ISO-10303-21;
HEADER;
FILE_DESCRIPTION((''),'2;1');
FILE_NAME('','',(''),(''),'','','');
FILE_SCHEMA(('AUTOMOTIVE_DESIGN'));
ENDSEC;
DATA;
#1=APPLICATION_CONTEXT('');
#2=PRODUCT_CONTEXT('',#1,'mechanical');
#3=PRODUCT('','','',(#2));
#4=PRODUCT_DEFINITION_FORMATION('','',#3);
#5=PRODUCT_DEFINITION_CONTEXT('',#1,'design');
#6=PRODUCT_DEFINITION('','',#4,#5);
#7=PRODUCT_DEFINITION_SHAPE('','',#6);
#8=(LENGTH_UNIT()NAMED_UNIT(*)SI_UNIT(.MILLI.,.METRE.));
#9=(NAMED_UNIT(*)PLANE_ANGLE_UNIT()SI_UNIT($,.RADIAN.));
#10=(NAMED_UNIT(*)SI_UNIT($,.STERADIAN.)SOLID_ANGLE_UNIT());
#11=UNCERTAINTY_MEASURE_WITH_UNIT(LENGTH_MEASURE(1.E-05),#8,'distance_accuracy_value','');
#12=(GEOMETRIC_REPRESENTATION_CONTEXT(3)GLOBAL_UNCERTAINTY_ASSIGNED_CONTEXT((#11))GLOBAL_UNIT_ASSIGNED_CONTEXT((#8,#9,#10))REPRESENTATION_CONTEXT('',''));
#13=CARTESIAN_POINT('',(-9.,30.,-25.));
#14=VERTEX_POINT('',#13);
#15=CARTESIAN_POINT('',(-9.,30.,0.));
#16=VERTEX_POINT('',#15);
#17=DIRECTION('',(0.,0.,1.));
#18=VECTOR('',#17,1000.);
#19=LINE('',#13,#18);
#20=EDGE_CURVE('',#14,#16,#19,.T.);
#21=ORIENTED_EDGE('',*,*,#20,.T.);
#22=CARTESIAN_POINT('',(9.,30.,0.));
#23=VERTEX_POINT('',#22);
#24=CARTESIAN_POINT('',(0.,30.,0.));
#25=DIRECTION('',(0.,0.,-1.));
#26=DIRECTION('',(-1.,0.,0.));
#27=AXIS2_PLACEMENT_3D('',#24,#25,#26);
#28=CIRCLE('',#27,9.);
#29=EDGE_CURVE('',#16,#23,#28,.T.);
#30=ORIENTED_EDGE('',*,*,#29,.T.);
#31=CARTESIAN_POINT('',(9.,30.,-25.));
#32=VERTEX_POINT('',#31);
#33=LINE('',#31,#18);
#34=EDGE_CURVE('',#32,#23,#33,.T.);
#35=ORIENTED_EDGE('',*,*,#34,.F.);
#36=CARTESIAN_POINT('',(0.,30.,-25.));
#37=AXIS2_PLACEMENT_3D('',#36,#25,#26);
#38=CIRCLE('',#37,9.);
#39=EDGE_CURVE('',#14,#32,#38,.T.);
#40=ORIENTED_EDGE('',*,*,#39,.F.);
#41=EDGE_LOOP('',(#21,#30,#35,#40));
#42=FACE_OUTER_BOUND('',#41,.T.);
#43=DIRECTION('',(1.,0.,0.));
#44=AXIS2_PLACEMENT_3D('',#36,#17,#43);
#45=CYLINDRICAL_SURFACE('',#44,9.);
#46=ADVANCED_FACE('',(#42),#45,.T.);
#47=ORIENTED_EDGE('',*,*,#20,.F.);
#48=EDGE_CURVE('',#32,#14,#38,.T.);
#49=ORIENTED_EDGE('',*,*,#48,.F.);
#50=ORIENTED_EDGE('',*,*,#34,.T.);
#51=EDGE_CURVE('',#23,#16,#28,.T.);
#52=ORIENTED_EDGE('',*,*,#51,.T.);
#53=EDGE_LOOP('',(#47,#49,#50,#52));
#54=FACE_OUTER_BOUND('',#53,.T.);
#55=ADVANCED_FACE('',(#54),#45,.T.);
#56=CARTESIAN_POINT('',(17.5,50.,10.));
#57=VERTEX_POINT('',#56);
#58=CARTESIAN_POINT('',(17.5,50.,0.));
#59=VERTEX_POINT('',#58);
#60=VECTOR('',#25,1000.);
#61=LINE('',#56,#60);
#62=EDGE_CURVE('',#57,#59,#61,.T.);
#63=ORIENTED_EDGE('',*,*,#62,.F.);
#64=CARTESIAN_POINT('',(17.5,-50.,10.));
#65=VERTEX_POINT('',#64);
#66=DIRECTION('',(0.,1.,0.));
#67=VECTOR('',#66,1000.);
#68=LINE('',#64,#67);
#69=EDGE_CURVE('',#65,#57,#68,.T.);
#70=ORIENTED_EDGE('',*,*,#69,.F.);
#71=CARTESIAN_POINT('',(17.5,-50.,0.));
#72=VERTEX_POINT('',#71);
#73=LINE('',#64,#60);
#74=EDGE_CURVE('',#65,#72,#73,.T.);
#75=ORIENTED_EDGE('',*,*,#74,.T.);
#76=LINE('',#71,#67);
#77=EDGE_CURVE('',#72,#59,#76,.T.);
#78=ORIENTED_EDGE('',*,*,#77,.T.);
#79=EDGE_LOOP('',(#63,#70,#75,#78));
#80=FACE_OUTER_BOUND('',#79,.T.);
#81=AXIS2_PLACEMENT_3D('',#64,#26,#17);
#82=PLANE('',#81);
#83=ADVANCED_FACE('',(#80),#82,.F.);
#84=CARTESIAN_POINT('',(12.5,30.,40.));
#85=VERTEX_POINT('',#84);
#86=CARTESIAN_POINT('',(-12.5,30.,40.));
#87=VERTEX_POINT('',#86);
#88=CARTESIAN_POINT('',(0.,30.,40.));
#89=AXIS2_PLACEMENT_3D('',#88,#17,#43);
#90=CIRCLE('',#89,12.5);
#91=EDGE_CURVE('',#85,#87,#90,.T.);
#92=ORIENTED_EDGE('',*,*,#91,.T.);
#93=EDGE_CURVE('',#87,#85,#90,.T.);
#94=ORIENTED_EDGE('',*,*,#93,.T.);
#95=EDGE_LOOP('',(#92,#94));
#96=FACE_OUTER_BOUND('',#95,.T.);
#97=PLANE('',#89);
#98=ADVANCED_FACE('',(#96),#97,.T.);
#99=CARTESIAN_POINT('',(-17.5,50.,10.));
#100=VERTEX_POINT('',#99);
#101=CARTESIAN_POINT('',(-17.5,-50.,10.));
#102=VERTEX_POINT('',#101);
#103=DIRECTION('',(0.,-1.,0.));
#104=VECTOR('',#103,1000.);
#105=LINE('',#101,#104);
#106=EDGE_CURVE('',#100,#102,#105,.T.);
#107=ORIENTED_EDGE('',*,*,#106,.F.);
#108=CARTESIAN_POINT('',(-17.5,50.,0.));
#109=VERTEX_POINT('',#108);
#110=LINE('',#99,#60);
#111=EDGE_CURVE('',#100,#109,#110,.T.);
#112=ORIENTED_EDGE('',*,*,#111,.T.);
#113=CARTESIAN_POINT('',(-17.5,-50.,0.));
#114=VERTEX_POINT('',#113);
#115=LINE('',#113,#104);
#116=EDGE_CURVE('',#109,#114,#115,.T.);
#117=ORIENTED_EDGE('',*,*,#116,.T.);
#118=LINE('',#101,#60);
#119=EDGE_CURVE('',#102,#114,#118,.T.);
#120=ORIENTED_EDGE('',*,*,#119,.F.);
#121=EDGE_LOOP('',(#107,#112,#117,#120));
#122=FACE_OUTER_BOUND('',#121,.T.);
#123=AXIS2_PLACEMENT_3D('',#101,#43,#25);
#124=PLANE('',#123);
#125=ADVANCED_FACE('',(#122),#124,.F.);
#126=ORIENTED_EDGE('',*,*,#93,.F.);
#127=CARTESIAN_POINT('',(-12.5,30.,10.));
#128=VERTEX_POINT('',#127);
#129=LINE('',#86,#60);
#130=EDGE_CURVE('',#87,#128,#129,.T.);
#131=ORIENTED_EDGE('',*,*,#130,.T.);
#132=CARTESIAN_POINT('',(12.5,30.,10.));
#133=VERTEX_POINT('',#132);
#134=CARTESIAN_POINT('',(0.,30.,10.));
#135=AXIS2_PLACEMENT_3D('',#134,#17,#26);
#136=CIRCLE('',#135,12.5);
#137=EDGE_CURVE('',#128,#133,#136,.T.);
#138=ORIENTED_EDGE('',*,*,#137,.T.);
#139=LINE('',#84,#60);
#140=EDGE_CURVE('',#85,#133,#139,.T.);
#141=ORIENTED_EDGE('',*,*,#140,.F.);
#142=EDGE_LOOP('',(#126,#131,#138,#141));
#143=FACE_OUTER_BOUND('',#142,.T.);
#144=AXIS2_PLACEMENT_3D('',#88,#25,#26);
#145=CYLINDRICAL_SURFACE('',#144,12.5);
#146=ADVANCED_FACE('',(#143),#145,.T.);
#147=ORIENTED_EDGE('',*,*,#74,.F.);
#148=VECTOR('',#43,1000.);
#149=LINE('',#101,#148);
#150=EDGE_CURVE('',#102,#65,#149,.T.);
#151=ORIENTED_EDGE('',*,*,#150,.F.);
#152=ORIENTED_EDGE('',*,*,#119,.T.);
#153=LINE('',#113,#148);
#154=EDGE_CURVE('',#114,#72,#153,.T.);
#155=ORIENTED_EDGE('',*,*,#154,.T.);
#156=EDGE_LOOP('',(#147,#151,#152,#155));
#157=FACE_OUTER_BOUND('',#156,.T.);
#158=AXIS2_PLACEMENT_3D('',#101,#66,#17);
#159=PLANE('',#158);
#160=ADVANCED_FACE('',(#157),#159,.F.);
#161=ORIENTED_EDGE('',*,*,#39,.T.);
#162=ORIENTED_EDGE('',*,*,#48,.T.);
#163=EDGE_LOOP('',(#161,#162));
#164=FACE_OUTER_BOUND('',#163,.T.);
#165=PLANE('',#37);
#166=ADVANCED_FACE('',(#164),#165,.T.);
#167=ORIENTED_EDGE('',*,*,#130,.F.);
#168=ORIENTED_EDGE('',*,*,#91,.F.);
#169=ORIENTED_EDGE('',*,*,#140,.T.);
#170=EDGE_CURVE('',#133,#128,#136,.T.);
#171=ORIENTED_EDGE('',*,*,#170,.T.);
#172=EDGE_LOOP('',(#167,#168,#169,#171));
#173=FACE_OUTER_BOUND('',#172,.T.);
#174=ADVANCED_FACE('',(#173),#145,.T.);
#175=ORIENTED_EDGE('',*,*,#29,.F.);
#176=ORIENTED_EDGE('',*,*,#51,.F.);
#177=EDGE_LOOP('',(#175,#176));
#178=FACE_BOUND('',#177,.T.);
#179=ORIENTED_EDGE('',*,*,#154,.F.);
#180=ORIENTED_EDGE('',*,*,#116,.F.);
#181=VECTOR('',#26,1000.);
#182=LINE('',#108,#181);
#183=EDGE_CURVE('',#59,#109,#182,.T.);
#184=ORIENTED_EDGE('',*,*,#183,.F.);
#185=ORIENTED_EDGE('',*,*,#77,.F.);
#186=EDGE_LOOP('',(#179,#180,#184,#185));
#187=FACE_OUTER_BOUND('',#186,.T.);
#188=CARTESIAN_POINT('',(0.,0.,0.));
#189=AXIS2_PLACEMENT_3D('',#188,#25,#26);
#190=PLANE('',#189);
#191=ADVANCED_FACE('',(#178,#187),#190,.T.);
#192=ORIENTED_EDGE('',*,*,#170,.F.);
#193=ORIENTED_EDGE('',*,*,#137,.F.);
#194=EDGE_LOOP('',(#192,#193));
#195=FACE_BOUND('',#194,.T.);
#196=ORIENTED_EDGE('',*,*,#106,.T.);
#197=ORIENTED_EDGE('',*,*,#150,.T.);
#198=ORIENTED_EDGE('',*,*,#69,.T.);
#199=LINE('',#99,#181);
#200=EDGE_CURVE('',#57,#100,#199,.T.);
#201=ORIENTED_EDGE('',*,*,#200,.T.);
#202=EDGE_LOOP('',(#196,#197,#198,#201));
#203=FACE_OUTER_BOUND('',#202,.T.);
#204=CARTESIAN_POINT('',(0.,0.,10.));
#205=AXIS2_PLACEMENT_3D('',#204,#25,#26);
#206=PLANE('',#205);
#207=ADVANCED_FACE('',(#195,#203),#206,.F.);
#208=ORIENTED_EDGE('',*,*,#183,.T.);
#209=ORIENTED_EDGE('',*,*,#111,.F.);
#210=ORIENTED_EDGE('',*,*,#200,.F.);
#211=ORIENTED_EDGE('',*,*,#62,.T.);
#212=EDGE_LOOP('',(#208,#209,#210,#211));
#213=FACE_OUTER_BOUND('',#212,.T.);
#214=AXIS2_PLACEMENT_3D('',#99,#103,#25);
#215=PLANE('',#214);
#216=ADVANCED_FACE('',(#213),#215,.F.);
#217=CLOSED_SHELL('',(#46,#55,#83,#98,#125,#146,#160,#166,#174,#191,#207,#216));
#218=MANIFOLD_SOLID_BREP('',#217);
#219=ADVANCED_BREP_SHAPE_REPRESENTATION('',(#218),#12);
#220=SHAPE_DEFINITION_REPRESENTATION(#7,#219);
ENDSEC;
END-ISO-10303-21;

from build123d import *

# Parameters (mm, degrees)
SKETCH_1_W      = 35
SKETCH_1_H      = 100
EXTRUDE_1_DEPTH = 10
SKETCH_2_R      = 12.5
EXTRUDE_2_DEPTH = 30
SKETCH_3_R      = 9
EXTRUDE_3_DEPTH = 25


with BuildPart() as part:
    # 草图1 → 凸台-拉伸1 (new body)
    with BuildSketch(Plane.XY):
        Rectangle(SKETCH_1_W, SKETCH_1_H)
    extrude(amount=EXTRUDE_1_DEPTH)

    # 草图2 → 凸台-拉伸2 (add)
    with BuildSketch(Plane.XY.offset(10)):
        with Locations(Location((0, 30, 0), (0, 0, 180))):
            Circle(SKETCH_2_R)
    extrude(amount=EXTRUDE_2_DEPTH)

    # 草图3 → 凸台-拉伸3 (add)
    with BuildSketch(Plane(origin=(0, 0, 0), x_dir=(-1, 0, 0), z_dir=(0, 0, -1))):
        with Locations((0, 30)):
            Circle(SKETCH_3_R)
    extrude(amount=EXTRUDE_3_DEPTH)


solid = part.part
